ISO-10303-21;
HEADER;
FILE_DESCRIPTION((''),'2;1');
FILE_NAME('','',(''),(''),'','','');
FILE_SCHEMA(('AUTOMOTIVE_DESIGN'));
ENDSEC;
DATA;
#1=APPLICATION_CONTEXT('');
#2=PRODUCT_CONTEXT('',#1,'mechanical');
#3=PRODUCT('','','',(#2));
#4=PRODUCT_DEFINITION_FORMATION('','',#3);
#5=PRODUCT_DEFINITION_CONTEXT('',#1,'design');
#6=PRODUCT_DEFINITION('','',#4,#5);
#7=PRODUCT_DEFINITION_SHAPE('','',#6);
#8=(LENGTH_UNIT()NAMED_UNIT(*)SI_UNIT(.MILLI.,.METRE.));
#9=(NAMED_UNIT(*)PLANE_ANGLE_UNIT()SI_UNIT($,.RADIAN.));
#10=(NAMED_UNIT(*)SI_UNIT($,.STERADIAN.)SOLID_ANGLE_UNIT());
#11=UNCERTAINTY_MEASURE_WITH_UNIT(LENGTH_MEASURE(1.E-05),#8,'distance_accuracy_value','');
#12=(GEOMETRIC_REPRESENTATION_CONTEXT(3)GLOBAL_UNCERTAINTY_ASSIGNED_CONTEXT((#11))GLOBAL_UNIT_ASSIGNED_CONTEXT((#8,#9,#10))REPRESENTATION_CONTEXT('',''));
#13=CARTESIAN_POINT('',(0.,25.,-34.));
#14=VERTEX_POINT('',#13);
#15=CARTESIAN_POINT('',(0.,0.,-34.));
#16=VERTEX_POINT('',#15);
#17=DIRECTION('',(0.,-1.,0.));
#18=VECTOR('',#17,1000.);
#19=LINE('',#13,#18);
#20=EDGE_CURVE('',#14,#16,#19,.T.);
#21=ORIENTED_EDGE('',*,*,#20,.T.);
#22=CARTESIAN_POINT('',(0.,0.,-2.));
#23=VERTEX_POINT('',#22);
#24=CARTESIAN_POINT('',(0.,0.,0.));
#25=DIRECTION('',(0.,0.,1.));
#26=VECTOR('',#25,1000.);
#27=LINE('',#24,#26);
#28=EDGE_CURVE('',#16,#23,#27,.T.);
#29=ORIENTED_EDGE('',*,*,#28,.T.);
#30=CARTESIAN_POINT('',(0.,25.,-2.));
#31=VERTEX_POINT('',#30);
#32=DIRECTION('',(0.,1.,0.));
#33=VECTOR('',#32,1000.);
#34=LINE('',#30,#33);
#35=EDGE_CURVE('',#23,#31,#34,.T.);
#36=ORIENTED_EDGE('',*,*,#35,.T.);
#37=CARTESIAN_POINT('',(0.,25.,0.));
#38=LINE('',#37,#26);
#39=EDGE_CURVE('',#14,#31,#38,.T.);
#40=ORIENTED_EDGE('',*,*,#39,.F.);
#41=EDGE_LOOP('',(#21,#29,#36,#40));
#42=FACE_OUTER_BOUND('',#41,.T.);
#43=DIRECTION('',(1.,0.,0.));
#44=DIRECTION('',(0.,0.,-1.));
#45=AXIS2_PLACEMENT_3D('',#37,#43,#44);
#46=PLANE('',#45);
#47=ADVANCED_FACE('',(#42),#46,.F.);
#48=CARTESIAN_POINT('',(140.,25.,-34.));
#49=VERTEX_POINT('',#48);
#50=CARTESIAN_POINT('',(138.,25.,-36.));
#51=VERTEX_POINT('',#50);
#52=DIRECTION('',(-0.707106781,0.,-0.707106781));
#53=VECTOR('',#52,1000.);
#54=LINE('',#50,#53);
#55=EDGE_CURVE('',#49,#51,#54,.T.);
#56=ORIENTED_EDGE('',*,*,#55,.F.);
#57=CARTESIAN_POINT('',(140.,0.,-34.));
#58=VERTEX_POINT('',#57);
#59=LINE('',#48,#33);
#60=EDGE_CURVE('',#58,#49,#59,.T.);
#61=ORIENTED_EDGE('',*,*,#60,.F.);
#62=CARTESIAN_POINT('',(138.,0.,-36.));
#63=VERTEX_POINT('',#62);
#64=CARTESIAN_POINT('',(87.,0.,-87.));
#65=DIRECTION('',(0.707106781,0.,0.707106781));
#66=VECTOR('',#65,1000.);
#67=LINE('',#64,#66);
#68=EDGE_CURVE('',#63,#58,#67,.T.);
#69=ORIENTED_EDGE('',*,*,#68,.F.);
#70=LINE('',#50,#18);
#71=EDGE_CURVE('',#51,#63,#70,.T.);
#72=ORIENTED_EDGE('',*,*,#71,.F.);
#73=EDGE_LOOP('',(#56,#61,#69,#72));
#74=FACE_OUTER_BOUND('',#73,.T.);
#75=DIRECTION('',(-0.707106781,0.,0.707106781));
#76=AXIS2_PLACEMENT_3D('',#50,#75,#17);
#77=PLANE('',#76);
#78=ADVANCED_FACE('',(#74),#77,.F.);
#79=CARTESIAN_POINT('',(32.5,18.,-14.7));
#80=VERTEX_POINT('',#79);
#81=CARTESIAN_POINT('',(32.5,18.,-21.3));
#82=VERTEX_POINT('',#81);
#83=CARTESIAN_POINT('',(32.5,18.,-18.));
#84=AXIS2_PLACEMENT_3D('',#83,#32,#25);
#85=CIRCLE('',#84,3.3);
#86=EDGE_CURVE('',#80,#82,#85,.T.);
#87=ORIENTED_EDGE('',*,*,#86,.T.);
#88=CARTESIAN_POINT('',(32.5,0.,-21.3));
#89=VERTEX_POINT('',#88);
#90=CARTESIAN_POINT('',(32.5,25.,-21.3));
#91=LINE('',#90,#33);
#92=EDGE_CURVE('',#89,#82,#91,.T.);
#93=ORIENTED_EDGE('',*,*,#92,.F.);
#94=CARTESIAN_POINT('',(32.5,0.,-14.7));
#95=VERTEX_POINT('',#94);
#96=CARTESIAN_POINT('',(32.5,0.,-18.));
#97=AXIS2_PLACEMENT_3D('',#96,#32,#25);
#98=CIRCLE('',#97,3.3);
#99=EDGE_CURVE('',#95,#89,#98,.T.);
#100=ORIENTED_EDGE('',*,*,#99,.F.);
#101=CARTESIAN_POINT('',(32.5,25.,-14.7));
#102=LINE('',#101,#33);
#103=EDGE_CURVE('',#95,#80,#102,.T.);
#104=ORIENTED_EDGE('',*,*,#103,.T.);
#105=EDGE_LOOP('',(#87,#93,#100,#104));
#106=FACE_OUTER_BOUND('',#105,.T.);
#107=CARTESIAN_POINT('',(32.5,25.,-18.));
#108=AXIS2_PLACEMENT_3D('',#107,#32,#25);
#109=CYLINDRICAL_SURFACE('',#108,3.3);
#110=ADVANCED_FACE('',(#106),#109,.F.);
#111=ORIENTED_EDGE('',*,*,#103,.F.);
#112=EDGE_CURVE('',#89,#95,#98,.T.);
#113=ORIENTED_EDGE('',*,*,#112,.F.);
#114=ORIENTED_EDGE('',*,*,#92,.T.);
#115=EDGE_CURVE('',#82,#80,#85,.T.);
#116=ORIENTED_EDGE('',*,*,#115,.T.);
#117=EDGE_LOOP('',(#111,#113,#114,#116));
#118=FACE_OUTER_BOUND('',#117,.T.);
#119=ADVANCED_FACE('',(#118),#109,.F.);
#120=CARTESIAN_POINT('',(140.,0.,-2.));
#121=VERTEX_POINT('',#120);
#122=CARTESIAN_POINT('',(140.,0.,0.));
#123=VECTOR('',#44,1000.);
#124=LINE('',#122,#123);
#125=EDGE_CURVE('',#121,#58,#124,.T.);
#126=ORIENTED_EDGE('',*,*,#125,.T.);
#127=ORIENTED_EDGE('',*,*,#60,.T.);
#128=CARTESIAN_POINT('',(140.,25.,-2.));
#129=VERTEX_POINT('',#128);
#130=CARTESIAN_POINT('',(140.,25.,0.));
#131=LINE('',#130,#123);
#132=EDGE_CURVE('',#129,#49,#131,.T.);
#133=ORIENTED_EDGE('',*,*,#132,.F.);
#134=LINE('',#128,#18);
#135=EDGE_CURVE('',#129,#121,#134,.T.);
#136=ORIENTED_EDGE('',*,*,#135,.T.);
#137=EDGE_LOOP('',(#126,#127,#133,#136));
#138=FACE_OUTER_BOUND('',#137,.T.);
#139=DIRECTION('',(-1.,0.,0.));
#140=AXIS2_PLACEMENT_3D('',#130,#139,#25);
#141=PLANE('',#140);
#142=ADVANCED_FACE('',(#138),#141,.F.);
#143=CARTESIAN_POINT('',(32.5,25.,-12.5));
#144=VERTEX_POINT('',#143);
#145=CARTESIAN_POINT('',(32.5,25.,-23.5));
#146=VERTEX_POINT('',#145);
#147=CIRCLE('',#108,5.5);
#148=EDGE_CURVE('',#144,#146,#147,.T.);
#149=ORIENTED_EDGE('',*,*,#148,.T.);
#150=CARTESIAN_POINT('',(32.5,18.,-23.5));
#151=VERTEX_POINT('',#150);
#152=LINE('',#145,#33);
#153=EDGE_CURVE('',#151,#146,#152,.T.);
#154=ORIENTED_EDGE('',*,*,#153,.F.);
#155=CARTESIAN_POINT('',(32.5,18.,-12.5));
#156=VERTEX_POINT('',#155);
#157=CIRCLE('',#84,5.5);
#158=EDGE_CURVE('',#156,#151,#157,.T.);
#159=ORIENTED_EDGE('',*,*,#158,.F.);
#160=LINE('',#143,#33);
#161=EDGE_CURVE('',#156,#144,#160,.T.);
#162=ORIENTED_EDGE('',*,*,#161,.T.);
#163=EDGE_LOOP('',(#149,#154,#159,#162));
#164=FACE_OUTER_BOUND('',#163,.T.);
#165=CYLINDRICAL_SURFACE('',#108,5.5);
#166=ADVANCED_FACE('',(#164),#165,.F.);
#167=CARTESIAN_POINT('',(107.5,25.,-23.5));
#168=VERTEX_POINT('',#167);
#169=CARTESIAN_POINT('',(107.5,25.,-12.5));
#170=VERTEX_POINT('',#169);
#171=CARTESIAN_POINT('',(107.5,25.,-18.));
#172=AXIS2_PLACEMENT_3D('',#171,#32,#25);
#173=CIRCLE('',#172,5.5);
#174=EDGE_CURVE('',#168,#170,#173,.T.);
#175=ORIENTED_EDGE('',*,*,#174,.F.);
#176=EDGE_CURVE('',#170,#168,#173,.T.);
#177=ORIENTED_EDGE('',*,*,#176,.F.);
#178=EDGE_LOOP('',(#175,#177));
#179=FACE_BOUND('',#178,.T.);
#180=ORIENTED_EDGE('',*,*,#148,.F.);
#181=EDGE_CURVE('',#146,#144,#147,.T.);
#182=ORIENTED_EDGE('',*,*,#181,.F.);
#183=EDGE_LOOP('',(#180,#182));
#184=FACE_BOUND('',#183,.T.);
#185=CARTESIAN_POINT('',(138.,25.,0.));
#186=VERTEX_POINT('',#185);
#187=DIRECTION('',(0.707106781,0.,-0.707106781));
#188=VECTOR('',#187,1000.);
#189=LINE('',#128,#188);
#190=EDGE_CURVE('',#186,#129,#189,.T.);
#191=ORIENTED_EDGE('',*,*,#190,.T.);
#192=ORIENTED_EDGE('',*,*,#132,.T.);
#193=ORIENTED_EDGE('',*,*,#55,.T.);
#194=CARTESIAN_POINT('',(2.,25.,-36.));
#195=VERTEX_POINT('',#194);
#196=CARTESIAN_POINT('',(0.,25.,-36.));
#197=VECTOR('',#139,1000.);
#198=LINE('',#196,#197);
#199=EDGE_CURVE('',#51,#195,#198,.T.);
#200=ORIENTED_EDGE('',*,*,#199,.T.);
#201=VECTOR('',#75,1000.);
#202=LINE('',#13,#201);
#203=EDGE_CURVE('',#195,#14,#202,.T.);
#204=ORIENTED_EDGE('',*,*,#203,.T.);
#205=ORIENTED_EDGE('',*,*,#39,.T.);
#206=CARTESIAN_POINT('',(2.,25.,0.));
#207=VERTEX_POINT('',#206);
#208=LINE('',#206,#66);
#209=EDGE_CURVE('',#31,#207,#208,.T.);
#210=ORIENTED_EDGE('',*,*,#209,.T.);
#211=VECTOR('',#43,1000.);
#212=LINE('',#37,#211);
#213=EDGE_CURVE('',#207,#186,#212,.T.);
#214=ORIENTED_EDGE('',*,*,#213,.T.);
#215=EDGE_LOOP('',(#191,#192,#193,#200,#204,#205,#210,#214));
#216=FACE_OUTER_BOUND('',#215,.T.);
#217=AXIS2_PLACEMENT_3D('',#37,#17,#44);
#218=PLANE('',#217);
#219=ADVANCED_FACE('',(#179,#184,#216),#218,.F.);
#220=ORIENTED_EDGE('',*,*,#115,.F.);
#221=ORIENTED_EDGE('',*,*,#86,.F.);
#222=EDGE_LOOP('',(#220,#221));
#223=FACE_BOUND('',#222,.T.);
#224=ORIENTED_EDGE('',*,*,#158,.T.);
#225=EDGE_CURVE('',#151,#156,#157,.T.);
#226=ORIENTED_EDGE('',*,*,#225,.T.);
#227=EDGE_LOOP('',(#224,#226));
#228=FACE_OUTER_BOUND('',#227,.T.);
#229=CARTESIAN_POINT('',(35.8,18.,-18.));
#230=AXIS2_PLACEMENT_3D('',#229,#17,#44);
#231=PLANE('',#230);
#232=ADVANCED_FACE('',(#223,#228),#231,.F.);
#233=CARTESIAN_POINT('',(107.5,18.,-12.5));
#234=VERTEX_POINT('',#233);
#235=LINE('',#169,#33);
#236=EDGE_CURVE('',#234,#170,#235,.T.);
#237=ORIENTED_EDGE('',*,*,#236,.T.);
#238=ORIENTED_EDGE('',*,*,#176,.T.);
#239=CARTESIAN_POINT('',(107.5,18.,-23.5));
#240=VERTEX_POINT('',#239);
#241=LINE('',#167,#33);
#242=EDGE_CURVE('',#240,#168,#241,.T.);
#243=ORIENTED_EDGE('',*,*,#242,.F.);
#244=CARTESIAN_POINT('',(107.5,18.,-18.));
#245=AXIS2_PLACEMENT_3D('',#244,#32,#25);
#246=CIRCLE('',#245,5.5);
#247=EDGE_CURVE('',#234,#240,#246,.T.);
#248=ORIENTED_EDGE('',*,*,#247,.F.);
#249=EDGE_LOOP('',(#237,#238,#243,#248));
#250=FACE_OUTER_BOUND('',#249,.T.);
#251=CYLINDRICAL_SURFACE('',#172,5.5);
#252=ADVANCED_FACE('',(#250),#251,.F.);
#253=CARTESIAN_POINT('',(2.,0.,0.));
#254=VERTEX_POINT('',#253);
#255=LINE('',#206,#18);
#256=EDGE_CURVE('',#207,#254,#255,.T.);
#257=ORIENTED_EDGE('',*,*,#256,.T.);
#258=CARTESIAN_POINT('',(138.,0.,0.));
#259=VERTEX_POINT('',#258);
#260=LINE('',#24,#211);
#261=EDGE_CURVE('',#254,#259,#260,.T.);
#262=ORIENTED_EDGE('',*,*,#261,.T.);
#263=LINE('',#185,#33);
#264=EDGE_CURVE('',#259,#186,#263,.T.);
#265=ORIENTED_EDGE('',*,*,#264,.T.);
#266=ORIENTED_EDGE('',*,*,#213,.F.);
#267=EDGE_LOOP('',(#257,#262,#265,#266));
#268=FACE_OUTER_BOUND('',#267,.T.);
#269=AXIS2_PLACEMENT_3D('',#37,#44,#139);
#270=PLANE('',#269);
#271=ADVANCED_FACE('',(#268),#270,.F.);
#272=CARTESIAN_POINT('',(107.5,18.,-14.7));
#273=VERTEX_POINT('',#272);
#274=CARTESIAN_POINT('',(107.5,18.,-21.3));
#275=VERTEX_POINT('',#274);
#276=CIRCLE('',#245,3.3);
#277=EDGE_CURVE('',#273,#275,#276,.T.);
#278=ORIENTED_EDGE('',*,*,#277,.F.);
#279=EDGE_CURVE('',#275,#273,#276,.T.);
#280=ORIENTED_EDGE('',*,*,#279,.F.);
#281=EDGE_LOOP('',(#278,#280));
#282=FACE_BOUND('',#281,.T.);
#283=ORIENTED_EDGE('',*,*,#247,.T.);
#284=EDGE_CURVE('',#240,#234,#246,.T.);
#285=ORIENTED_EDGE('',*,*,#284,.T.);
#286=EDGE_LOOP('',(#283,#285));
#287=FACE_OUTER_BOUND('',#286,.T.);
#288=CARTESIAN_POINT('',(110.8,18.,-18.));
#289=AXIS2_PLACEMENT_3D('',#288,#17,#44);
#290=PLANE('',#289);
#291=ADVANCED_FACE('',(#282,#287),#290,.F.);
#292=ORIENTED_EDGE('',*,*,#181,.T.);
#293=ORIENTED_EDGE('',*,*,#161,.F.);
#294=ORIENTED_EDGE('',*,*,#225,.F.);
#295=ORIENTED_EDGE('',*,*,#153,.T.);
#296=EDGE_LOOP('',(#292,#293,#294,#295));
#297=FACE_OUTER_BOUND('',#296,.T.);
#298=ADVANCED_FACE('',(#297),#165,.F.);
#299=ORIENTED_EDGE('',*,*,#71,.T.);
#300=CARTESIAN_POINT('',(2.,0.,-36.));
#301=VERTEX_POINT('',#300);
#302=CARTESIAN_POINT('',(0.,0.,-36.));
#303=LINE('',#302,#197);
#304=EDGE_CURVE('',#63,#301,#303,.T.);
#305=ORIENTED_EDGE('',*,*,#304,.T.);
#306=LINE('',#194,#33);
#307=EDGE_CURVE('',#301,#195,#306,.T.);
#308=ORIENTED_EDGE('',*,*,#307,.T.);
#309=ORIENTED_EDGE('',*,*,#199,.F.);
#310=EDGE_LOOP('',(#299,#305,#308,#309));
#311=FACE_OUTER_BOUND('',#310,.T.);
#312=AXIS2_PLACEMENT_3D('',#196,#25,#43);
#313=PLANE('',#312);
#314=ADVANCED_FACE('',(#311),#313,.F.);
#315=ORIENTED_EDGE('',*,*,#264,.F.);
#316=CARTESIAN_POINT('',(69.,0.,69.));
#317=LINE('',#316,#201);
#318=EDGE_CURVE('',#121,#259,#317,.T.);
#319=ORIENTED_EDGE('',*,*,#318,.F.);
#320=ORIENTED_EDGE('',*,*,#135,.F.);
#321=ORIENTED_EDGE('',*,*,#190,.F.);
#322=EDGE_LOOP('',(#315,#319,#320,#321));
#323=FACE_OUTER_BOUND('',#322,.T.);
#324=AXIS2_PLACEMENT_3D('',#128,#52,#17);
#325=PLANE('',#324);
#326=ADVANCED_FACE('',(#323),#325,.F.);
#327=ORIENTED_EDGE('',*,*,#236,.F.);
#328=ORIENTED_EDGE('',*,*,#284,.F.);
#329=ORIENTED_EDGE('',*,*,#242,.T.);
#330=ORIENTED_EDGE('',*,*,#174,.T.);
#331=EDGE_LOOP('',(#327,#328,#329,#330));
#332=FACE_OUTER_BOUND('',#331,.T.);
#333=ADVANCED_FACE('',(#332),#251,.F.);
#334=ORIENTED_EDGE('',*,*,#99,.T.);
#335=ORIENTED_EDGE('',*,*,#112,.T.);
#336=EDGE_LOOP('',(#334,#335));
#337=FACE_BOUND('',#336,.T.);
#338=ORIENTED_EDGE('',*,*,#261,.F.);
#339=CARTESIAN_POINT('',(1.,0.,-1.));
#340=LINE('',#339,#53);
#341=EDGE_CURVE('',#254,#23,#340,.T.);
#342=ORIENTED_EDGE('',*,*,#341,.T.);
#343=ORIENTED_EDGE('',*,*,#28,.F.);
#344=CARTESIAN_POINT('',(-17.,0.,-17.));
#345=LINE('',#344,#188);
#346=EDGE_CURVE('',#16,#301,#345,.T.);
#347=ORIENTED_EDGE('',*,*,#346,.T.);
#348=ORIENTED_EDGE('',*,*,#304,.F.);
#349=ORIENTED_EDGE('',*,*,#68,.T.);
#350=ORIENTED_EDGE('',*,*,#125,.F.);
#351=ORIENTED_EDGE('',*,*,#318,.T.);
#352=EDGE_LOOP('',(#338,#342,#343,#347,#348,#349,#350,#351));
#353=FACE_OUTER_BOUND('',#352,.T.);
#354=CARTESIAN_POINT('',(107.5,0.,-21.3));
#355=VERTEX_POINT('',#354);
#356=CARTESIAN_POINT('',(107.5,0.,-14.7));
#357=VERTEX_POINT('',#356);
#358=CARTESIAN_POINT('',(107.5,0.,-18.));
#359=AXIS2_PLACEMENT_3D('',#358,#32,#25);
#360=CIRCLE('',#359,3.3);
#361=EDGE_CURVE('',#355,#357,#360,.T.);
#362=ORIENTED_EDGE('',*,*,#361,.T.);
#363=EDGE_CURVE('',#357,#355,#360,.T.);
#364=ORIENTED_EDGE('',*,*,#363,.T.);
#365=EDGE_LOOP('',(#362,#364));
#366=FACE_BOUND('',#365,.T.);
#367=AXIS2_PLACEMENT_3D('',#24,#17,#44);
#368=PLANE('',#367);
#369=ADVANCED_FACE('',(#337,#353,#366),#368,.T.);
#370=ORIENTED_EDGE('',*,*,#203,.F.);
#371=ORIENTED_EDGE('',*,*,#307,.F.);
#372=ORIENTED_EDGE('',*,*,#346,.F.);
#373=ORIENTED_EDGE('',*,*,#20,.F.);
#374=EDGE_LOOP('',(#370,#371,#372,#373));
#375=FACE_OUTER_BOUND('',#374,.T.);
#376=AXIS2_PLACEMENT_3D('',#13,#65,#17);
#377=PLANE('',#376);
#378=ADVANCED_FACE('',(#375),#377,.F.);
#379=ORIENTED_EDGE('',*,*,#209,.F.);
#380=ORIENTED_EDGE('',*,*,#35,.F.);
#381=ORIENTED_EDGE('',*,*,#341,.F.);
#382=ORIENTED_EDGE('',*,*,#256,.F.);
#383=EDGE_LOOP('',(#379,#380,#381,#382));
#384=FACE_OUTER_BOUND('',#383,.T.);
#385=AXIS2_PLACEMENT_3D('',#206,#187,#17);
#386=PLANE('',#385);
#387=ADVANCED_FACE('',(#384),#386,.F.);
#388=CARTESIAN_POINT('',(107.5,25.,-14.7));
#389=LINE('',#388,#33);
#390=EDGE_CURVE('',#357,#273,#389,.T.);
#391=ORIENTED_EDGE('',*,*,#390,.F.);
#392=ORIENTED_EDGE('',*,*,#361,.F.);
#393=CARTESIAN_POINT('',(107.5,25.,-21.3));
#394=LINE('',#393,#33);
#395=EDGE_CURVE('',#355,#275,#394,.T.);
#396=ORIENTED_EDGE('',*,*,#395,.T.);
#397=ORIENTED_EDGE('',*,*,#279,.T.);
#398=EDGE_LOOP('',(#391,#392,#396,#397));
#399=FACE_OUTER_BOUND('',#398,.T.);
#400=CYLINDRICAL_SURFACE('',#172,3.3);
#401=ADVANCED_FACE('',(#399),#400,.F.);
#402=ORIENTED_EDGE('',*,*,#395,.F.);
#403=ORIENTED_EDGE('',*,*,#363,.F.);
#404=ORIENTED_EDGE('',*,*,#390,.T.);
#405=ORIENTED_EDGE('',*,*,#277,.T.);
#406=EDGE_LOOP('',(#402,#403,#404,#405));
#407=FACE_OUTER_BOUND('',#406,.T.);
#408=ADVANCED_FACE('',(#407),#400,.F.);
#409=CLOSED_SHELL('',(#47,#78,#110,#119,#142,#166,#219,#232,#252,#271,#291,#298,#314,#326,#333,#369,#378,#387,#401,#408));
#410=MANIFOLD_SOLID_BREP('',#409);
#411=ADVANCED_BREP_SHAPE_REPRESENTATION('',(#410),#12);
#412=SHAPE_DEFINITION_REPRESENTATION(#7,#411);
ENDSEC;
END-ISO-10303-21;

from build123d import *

# Parameters (mm, degrees)
SKETCH_1_W                = 140
SKETCH_1_H                = 36
EXTRUDE_1_DEPTH           = 25
HOLE_WIZARD_1_D           = 6.6
HOLE_WIZARD_1_CBORE_D     = 11
HOLE_WIZARD_1_CBORE_DEPTH = 7
CHAMFER_1_SIZE            = 2


with BuildPart() as part:
    # 草图1 → 凸台-拉伸1 (new body)
    with BuildSketch(Plane(origin=(0, 0, 0), x_dir=(1, 0, 0), z_dir=(0, 1, 0))):
        with Locations((70, 18)):
            Rectangle(SKETCH_1_W, SKETCH_1_H)
    extrude(amount=EXTRUDE_1_DEPTH)

    # 打孔尺寸(%根据)内六角圆柱头螺钉的类型1 (through all)
    with Locations(Plane(origin=(0, 25, 0), x_dir=(1, 0, 0), z_dir=(0, 1, 0))):
        with Locations((32.5, 18), (107.5, 18)):
            CounterBoreHole(HOLE_WIZARD_1_D / 2, HOLE_WIZARD_1_CBORE_D / 2, HOLE_WIZARD_1_CBORE_DEPTH)

    # 倒角1
    chamfer_1_edges = [part.edges().sort_by_distance(p)[0] for p in [
        (0, 12.5, -36),
        (140, 12.5, -36),
        (140, 12.5, 0),
        (0, 12.5, 0),
    ]]
    chamfer(chamfer_1_edges, length=CHAMFER_1_SIZE)


solid = part.part
